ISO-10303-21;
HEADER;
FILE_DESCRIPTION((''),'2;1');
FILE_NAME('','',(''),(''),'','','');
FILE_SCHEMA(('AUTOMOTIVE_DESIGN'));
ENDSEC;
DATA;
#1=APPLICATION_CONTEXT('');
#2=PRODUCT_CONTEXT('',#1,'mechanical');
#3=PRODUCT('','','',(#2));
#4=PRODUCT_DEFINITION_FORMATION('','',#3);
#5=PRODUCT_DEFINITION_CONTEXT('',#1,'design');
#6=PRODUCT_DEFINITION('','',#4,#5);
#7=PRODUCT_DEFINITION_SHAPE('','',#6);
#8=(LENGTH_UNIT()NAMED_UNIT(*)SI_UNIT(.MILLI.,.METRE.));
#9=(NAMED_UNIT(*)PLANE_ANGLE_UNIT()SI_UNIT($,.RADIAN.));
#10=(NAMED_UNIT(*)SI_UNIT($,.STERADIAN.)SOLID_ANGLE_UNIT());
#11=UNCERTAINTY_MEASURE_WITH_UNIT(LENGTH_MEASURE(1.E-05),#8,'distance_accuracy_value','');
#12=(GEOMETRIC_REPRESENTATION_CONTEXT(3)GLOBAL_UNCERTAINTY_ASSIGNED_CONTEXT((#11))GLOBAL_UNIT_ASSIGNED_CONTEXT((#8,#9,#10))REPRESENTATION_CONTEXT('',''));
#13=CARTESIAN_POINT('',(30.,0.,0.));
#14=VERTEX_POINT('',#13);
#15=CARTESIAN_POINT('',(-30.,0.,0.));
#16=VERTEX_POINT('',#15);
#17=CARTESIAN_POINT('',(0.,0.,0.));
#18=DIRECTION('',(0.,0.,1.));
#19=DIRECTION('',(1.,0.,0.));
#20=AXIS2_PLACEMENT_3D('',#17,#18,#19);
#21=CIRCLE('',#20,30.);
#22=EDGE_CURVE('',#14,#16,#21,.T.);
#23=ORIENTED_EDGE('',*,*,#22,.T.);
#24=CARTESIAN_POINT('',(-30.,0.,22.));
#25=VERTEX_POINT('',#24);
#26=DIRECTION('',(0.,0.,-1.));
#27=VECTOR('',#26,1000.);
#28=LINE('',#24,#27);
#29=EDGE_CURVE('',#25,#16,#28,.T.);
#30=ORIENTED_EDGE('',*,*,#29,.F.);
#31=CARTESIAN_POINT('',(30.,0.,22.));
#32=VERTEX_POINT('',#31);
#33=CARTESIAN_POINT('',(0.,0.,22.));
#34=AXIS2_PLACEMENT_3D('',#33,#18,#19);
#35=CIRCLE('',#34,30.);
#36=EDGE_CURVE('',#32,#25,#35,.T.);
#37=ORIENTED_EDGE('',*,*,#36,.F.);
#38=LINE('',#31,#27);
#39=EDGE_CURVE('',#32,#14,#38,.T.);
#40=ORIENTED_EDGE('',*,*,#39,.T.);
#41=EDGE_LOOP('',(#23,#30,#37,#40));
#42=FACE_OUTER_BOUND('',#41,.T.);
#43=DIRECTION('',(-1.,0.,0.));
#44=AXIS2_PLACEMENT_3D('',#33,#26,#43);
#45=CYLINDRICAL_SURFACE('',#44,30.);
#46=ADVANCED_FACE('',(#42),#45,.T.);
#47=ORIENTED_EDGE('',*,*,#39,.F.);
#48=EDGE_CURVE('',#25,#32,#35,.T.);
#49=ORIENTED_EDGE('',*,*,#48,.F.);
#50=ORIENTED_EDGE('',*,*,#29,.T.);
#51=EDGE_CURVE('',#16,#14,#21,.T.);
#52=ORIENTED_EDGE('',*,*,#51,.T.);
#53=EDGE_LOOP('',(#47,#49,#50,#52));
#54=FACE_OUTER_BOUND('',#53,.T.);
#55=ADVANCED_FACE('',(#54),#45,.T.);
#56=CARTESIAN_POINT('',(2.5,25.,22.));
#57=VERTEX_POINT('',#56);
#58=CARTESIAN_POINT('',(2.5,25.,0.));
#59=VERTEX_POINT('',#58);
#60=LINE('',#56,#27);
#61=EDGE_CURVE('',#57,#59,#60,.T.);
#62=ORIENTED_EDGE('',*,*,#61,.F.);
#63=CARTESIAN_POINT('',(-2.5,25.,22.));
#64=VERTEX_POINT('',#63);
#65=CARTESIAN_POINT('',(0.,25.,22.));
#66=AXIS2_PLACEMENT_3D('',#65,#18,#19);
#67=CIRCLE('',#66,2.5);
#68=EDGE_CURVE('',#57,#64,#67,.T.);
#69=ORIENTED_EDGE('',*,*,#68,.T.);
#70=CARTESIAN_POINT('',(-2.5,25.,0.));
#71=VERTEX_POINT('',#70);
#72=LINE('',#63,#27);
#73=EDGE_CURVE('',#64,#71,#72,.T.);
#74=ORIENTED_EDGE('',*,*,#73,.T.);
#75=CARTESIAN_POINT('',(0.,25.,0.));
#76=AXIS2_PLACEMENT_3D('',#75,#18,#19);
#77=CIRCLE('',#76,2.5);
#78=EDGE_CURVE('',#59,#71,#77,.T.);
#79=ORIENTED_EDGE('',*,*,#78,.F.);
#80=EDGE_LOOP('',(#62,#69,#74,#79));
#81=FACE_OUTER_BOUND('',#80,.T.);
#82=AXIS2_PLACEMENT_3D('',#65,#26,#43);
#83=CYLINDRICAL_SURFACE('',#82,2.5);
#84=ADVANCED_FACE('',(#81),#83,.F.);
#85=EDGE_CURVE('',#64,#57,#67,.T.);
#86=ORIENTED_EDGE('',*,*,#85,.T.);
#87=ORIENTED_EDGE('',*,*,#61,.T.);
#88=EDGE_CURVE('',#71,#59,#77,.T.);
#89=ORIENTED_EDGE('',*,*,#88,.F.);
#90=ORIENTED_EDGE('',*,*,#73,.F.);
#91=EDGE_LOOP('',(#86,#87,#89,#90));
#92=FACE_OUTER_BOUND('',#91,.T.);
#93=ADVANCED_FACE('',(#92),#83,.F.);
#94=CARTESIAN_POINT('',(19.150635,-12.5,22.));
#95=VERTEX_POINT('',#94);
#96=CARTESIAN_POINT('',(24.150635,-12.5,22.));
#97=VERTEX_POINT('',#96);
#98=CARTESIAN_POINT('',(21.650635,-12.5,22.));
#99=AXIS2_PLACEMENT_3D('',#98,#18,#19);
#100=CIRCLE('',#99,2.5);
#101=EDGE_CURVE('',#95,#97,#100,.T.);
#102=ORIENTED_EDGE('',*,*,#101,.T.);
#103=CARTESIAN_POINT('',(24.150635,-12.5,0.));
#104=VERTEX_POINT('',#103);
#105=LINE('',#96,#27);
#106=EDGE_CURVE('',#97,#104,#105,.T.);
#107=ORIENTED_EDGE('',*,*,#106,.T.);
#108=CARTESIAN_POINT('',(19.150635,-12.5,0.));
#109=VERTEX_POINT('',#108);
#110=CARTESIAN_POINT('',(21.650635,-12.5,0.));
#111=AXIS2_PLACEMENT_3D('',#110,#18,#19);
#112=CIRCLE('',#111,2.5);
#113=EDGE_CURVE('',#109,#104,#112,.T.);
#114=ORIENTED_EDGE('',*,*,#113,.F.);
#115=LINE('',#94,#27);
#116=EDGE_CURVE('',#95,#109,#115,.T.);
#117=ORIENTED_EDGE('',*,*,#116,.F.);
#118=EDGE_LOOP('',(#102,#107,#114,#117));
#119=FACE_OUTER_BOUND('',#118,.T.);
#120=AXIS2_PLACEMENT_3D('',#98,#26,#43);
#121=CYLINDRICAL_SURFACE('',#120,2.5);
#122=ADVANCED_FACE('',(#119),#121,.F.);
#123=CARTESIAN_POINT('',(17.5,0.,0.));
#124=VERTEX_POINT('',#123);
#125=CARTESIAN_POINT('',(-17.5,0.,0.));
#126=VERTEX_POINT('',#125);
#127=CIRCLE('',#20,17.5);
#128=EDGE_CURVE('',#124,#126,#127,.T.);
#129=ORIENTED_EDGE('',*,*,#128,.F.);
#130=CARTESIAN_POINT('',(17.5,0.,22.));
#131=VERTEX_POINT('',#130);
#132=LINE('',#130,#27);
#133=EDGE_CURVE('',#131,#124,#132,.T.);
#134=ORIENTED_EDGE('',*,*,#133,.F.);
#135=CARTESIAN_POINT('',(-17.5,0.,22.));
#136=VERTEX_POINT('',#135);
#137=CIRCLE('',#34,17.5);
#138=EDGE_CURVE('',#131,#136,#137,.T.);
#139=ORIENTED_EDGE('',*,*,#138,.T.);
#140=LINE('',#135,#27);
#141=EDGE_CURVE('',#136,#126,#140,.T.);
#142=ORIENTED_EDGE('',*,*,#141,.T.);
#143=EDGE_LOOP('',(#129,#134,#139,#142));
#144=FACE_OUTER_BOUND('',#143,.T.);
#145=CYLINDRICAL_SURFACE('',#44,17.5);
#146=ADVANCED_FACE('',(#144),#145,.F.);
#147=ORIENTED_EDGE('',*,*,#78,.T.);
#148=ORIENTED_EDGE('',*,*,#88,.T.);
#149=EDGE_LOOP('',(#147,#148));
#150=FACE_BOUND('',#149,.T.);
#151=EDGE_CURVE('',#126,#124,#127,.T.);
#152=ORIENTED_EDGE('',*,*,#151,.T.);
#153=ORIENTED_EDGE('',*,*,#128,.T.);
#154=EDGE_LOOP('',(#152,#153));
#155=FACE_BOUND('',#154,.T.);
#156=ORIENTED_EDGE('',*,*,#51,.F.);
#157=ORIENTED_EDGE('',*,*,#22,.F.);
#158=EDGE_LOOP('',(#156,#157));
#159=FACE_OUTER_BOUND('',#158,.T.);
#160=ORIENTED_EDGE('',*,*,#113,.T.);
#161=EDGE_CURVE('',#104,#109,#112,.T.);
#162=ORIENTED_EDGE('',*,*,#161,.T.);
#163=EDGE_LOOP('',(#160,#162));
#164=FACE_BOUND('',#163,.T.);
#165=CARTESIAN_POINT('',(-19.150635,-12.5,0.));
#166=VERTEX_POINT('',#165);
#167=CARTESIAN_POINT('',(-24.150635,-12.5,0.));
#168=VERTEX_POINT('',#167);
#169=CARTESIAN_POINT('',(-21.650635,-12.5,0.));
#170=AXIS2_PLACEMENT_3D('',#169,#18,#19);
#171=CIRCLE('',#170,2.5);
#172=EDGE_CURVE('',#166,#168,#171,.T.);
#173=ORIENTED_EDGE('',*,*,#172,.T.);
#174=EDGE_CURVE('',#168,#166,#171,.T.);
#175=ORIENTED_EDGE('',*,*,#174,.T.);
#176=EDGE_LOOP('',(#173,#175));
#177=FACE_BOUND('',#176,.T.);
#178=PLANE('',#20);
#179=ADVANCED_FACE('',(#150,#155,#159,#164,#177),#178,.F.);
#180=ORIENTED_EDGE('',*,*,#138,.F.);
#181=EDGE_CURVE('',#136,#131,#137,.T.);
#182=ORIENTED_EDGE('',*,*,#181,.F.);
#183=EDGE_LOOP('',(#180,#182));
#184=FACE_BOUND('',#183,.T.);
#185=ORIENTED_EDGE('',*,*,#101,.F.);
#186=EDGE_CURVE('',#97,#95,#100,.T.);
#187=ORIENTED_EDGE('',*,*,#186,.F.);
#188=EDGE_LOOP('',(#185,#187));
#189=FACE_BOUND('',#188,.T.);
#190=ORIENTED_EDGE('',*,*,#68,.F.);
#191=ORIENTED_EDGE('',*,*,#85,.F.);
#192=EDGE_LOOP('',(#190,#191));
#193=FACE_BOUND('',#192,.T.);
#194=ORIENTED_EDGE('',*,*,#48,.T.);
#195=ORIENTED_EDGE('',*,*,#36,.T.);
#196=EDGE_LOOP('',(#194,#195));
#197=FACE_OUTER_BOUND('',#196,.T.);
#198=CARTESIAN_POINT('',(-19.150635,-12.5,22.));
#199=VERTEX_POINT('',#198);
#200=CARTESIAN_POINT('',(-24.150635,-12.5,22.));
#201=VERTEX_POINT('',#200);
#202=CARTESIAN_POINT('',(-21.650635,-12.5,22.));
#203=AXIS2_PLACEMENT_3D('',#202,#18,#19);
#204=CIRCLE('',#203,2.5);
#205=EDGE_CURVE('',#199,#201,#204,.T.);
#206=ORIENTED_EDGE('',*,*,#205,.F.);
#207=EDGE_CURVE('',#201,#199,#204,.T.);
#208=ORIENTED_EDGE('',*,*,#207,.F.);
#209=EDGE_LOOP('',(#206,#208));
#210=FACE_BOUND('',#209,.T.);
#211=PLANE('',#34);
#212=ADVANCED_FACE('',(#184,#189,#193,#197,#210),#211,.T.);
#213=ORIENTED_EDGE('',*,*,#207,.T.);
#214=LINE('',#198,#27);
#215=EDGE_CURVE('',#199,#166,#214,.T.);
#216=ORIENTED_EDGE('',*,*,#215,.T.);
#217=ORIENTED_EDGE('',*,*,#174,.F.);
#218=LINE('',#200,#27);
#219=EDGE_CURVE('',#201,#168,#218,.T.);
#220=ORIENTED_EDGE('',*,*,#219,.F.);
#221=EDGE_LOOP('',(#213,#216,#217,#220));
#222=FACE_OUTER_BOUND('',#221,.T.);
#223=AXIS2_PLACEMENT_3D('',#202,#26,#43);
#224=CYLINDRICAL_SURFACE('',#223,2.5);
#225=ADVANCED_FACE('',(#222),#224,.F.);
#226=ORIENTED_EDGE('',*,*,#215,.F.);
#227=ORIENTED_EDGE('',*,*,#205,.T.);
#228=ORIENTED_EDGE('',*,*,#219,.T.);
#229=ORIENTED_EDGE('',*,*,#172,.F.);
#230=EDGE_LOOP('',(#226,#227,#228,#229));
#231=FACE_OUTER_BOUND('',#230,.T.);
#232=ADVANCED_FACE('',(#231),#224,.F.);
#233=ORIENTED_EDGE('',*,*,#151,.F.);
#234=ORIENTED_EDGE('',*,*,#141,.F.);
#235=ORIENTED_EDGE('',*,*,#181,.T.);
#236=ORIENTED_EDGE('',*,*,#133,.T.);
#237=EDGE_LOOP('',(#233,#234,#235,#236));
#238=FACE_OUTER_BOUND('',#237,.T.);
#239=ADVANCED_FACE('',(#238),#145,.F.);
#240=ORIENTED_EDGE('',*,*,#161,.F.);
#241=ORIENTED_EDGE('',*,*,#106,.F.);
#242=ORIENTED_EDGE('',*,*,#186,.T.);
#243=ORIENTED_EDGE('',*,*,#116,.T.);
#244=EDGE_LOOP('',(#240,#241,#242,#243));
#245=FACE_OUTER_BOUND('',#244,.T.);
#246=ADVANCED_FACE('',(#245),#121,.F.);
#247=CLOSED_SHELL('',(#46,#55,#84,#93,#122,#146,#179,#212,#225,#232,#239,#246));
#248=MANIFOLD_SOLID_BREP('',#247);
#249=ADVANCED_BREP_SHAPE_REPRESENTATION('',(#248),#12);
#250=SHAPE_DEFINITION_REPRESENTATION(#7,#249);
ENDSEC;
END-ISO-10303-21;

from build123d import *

# Parameters (mm, degrees)
SKETCH1_R           = 30
SKETCH1_R_2         = 17.5
SKETCH1_R_3         = 2.5
BOSS_EXTRUDE1_DEPTH = 22


with BuildPart() as part:
    # Sketch1 → Boss-Extrude1 (new body)
    with BuildSketch(Plane.XY):
        Circle(SKETCH1_R)
        Circle(SKETCH1_R_2, mode=Mode.SUBTRACT)
        with Locations((0, 25)):
            Circle(SKETCH1_R_3, mode=Mode.SUBTRACT)
        with Locations((21.650635095, -12.5)):
            Circle(SKETCH1_R_3, mode=Mode.SUBTRACT)
        with Locations((-21.650635095, -12.5)):
            Circle(SKETCH1_R_3, mode=Mode.SUBTRACT)
    extrude(amount=BOSS_EXTRUDE1_DEPTH)


solid = part.part
